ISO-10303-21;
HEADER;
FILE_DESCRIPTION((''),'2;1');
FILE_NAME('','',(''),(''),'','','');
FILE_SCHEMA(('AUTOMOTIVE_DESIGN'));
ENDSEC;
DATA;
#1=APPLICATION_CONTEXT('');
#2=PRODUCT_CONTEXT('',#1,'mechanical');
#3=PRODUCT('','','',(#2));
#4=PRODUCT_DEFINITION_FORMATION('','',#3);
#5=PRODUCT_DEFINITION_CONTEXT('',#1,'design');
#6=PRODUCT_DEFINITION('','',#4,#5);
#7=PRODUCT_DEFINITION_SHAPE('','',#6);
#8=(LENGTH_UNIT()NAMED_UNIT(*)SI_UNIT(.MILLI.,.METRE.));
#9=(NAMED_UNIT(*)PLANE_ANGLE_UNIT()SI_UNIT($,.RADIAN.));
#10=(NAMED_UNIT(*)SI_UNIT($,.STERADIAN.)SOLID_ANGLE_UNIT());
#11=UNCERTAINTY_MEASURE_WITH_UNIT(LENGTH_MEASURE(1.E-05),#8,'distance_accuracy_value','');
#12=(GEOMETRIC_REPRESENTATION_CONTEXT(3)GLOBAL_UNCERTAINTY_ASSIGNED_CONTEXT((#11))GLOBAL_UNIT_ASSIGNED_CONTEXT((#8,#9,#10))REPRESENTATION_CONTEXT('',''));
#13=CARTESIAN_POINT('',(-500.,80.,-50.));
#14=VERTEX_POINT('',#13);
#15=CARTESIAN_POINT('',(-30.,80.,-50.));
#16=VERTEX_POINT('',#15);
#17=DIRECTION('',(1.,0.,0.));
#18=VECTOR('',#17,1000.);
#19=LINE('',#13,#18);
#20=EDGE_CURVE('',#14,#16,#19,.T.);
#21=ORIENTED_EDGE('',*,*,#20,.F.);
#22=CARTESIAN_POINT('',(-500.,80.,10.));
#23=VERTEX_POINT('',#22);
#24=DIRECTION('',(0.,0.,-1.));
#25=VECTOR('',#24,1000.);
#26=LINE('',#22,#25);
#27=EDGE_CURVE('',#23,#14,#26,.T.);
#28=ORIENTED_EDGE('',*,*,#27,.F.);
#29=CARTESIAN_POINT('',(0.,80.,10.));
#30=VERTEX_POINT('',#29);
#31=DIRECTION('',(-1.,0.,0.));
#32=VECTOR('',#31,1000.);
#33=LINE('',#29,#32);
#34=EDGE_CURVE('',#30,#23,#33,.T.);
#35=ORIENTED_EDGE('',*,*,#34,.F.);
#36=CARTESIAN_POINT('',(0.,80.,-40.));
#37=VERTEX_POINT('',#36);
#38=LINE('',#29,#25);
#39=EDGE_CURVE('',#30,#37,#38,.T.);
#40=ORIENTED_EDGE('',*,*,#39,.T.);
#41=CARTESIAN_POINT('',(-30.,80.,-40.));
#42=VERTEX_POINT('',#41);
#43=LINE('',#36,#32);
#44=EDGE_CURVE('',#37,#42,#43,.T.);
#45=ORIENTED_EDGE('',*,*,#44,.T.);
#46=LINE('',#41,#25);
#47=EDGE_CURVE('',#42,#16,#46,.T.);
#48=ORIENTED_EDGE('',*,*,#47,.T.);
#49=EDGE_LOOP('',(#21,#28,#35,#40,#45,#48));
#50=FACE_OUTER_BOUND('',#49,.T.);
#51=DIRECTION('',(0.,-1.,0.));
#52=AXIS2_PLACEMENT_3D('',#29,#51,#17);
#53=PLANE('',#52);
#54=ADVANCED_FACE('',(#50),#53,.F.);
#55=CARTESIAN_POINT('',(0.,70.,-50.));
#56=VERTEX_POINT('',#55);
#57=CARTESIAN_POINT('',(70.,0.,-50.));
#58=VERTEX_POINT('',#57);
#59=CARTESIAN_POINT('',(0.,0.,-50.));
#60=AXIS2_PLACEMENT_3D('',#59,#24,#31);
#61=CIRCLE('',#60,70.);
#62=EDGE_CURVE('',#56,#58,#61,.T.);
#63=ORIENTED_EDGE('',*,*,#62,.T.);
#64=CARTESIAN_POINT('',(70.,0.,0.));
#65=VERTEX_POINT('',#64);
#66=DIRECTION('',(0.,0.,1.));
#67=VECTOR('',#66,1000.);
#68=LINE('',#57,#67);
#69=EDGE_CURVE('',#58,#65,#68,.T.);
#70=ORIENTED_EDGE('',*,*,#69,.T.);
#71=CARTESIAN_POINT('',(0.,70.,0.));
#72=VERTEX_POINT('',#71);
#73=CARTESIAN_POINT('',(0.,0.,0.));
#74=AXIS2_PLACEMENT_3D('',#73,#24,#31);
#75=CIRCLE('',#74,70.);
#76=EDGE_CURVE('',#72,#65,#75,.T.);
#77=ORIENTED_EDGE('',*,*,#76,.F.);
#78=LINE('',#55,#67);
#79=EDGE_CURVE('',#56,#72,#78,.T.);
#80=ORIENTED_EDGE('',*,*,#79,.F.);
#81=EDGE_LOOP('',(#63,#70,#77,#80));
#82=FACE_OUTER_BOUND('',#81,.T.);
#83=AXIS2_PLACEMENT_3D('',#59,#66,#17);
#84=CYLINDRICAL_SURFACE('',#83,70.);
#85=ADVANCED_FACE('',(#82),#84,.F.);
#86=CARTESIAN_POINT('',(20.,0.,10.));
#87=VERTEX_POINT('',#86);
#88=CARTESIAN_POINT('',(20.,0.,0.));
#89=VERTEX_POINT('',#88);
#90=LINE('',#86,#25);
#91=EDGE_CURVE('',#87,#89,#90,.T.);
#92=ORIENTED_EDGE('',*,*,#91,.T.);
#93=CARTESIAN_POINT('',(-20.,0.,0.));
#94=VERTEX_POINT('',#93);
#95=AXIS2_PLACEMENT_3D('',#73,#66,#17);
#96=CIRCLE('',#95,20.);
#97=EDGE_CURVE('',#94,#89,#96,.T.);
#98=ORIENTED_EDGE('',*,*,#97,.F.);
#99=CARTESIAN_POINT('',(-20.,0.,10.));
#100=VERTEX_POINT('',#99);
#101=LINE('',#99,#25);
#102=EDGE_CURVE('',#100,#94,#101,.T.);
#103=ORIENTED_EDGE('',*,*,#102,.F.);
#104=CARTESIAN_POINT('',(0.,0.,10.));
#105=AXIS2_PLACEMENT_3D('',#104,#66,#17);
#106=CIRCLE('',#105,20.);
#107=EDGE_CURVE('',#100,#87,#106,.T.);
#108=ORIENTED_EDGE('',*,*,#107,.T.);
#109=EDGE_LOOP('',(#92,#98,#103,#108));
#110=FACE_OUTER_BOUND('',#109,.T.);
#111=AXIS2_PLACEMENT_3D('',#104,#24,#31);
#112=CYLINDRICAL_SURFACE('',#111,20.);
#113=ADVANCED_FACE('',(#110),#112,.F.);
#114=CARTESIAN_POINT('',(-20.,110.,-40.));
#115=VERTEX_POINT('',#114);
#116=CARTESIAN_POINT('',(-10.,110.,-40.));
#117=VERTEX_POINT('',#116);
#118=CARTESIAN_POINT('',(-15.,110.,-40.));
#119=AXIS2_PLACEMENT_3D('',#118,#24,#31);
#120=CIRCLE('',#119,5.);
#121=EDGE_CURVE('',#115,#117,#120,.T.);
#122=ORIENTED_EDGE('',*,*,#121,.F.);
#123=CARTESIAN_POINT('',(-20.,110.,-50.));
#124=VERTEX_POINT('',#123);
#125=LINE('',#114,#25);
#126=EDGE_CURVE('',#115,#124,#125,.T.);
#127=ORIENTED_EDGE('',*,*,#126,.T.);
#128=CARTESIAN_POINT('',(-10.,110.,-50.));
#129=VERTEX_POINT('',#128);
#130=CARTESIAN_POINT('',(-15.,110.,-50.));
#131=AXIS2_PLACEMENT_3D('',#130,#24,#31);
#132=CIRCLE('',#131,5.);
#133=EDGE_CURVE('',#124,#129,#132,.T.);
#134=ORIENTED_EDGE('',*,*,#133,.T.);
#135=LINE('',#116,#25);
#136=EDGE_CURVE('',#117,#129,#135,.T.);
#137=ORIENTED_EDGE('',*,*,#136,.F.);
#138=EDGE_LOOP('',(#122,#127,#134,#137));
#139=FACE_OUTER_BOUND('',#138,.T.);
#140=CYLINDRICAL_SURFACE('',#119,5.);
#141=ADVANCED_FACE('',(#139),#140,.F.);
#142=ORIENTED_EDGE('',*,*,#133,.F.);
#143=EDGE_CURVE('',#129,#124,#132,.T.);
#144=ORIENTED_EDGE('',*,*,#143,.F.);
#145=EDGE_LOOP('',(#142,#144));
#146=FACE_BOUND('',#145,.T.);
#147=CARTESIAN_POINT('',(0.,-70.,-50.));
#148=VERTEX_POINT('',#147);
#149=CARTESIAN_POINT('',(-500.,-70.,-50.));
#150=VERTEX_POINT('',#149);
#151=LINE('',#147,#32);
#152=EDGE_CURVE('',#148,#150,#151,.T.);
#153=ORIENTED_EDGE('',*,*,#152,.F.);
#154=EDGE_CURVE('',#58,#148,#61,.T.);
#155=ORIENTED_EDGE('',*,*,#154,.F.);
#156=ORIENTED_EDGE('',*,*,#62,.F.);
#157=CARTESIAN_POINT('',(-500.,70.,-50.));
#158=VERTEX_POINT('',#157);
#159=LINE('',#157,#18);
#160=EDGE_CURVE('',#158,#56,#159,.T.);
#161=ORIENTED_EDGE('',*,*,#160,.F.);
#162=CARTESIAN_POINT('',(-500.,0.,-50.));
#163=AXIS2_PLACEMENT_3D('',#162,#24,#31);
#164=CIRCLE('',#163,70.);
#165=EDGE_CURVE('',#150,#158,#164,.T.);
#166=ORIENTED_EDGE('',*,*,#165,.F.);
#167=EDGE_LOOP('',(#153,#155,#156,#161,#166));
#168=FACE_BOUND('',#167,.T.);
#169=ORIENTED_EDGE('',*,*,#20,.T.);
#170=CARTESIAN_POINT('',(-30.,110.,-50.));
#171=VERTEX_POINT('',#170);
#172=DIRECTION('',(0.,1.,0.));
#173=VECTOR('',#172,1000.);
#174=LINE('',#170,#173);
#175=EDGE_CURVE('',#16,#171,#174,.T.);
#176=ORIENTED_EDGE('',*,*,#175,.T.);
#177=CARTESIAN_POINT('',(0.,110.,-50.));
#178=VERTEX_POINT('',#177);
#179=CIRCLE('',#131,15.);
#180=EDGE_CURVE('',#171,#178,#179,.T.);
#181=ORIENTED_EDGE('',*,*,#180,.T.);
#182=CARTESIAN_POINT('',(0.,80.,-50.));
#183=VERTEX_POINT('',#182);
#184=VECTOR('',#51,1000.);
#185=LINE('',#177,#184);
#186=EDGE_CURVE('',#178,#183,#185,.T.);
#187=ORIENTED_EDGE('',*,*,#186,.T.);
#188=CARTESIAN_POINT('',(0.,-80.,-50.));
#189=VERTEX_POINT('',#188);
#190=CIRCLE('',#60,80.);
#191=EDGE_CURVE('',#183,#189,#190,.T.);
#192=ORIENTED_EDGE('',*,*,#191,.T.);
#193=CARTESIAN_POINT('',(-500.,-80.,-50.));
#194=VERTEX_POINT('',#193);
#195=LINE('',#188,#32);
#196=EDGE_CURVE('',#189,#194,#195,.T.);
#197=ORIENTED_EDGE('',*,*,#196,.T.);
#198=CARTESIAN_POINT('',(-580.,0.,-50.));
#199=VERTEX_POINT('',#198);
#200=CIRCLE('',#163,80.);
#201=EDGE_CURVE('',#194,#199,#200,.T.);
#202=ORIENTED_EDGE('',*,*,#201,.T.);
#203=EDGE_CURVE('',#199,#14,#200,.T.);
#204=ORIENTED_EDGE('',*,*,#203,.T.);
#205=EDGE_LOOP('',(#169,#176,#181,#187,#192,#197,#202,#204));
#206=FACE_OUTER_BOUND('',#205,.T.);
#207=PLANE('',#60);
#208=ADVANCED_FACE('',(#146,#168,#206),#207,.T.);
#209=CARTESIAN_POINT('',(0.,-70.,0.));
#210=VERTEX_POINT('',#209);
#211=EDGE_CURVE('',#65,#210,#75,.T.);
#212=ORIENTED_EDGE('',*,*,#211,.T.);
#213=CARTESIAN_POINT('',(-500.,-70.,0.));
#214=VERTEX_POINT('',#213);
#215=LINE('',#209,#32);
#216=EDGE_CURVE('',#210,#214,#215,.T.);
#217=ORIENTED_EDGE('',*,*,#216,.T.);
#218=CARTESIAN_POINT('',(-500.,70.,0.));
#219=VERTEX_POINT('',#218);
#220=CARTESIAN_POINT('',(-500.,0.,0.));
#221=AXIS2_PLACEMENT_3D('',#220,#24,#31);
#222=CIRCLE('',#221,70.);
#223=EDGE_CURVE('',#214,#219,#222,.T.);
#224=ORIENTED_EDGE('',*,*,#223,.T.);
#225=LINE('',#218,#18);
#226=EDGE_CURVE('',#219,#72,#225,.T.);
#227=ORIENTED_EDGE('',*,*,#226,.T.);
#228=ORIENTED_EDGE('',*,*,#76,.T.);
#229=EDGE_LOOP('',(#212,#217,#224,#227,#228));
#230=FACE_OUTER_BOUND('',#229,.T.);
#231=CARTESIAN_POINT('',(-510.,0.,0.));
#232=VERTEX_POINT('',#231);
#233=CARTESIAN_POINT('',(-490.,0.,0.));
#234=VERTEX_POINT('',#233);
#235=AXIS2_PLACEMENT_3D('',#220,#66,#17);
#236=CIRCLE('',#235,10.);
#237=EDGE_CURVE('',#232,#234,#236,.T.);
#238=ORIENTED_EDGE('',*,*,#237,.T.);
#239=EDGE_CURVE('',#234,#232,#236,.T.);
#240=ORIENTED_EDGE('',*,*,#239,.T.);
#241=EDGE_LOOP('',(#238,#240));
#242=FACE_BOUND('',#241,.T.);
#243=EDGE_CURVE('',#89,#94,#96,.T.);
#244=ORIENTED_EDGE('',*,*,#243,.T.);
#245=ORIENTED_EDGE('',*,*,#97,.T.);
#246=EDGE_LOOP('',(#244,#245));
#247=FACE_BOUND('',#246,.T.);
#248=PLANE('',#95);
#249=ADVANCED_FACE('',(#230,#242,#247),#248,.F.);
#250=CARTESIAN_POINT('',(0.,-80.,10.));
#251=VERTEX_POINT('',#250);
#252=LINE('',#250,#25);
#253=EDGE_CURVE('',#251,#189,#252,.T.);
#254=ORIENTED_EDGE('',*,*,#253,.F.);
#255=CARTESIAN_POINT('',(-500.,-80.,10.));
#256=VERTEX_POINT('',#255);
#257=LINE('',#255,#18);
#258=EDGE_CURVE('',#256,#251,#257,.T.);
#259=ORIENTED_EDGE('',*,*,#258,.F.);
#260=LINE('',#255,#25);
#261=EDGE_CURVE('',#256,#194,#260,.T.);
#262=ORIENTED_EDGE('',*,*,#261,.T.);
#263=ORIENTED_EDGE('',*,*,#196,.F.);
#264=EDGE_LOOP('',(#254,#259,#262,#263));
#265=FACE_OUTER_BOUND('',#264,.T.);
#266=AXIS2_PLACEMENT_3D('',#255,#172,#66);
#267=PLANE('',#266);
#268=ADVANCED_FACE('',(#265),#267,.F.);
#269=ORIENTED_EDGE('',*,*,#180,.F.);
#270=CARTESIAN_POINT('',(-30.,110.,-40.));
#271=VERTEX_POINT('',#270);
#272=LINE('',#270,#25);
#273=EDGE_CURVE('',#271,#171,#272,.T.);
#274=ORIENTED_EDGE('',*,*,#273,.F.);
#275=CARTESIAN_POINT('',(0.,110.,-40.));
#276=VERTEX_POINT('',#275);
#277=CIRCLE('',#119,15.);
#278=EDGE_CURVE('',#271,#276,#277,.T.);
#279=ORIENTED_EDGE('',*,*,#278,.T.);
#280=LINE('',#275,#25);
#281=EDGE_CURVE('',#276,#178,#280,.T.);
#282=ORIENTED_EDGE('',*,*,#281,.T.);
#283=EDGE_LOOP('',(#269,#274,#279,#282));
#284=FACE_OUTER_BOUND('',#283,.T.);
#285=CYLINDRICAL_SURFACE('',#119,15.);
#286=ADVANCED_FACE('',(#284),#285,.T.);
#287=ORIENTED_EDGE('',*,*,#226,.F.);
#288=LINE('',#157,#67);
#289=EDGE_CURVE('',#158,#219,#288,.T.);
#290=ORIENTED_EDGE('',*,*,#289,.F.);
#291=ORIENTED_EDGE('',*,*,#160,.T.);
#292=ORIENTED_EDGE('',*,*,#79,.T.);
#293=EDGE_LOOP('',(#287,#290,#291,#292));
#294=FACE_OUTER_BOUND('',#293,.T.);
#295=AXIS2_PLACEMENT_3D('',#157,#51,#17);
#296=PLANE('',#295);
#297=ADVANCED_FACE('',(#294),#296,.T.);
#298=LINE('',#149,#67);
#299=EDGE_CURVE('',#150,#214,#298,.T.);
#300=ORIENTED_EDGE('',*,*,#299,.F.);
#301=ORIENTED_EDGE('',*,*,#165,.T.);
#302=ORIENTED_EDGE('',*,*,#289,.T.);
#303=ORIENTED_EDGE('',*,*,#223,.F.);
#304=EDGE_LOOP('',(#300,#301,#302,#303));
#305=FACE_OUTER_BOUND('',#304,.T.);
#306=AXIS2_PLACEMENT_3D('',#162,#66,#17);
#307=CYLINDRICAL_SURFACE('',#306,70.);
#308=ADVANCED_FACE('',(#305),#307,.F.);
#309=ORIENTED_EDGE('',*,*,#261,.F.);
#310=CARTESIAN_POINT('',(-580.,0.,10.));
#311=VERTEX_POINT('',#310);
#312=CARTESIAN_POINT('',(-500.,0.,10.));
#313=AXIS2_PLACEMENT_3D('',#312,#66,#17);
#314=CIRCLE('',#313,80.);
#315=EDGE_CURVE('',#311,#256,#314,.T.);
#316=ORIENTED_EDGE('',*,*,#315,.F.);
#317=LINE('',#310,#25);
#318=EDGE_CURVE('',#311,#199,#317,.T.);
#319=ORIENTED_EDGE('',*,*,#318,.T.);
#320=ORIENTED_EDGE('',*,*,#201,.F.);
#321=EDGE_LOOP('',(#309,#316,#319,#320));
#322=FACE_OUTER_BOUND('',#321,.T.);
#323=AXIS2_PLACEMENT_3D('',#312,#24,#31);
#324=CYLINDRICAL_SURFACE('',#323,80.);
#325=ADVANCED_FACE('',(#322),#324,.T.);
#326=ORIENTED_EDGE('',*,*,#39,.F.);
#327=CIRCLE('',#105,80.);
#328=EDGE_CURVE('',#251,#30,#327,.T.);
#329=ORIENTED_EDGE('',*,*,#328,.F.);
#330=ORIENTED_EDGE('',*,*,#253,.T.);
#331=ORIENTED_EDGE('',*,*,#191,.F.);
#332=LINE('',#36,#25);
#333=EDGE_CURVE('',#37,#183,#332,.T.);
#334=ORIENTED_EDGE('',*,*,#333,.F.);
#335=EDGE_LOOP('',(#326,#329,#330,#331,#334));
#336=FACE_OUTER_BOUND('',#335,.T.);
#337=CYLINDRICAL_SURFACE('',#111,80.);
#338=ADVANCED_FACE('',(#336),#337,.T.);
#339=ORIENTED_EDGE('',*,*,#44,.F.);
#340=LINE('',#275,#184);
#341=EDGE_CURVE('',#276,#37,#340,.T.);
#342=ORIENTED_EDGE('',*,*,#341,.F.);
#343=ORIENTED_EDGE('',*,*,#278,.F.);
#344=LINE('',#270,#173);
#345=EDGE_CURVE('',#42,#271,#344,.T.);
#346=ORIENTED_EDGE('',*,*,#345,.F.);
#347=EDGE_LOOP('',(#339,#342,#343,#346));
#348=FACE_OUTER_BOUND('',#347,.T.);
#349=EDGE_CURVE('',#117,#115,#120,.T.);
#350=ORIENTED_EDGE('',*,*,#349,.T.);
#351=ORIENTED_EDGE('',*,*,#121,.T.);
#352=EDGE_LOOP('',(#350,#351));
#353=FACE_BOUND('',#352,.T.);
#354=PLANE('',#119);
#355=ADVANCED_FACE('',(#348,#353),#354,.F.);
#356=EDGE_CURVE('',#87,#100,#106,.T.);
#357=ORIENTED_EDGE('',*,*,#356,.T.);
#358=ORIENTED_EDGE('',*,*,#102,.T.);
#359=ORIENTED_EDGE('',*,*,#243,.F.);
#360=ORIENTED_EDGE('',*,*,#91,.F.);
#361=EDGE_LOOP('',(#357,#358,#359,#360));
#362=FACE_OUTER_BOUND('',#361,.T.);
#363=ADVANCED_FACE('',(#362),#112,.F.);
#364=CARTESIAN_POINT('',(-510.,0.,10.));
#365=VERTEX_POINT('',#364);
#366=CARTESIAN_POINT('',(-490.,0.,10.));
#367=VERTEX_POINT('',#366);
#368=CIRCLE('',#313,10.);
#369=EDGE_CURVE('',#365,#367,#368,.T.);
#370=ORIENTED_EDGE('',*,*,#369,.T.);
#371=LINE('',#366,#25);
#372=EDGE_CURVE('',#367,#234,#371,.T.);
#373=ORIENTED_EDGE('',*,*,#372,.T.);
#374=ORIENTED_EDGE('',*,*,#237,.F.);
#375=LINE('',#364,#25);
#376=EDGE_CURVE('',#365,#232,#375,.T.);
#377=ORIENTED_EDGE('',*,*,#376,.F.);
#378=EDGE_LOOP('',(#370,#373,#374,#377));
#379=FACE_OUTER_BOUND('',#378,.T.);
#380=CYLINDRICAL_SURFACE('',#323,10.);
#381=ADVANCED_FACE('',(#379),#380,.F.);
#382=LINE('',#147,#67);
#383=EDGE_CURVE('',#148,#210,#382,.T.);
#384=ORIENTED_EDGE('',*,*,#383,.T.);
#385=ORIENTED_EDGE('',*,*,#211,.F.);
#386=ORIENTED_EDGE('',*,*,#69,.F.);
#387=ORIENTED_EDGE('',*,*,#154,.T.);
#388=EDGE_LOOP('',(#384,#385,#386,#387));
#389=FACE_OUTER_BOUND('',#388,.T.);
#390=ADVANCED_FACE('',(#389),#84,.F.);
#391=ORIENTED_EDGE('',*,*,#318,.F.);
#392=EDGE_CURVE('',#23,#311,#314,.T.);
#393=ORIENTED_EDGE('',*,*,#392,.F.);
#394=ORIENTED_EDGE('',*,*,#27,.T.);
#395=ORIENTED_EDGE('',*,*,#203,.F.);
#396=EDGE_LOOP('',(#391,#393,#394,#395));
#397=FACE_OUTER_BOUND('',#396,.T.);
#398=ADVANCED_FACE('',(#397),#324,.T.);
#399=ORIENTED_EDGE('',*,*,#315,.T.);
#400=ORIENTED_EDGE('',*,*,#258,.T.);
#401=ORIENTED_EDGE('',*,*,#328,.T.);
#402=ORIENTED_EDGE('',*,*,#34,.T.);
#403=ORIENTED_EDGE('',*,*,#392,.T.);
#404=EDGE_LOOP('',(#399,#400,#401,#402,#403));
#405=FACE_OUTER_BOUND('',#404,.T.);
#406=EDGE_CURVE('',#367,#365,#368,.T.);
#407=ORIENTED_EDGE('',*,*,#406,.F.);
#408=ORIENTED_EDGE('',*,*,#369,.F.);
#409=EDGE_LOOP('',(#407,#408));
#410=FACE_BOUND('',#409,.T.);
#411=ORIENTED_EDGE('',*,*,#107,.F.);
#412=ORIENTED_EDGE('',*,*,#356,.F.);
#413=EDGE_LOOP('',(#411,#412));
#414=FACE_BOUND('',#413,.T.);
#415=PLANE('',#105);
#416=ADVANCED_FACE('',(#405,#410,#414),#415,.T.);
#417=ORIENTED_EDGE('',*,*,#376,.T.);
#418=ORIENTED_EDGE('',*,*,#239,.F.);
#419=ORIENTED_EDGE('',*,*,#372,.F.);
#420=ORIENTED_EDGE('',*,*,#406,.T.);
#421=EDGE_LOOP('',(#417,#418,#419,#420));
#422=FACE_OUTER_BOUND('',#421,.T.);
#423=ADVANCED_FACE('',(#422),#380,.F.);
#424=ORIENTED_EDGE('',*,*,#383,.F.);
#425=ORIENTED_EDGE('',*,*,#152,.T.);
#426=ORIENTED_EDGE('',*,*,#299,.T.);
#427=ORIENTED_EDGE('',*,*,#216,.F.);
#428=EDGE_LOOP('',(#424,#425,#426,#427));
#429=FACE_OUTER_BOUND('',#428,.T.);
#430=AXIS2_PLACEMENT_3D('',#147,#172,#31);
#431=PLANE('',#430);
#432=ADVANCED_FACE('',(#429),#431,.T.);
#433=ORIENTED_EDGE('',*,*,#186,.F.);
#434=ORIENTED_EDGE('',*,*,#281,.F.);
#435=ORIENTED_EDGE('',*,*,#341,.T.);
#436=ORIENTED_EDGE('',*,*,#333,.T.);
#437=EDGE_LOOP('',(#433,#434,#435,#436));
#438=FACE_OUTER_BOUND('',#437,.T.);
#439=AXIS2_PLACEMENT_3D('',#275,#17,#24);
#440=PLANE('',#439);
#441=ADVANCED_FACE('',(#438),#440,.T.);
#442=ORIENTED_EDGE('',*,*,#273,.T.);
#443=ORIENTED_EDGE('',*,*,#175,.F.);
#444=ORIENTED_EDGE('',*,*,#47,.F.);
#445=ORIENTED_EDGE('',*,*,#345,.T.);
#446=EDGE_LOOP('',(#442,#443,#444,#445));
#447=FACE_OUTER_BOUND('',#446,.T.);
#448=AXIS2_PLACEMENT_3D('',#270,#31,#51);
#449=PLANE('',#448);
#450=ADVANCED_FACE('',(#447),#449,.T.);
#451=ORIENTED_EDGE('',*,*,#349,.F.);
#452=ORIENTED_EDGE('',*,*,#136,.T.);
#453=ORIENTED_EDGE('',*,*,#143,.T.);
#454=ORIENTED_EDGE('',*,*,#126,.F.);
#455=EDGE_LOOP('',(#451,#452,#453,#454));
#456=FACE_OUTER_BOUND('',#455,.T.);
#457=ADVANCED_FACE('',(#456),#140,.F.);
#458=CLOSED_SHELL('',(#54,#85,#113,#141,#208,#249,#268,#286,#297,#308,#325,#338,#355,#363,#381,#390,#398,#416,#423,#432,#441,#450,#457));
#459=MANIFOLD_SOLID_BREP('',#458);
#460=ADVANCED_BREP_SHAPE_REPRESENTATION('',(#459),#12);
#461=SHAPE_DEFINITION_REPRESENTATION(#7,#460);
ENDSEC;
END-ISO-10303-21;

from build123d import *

# Parameters (mm, degrees)
SKETCH_1_R      = 20
SKETCH_1_R_2    = 10
EXTRUDE_1_DEPTH = 10
EXTRUDE_START   = 50
EXTRUDE_2_DEPTH = 50
SKETCH_4_R      = 5
EXTRUDE_3_DEPTH = 10


with BuildPart() as part:
    # 草图1 → 凸台-拉伸1 (new body)
    with BuildSketch(Plane.XY):
        with BuildLine():
            Line((0, 80), (-500, 80))
            ThreePointArc((-500, 80), (-580, 0), (-500, -80))
            Line((-500, -80), (0, -80))
            ThreePointArc((0, -80), (80, 0), (0, 80))
        make_face()
        Circle(SKETCH_1_R, mode=Mode.SUBTRACT)
        with Locations((-500, 0)):
            Circle(SKETCH_1_R_2, mode=Mode.SUBTRACT)
    extrude(amount=EXTRUDE_1_DEPTH)

    # 草图2 → 凸台-拉伸2 (add)
    with BuildSketch(Plane(origin=(0, 0, 0), x_dir=(-1, 0, 0), z_dir=(0, 0, -1)).offset(EXTRUDE_START)):
        with BuildLine():
            Line((0, -80), (500, -80))
            ThreePointArc((500, -80), (580, 0), (500, 80))
            Line((500, 80), (0, 80))
            ThreePointArc((0, 80), (-80, 0), (0, -80))
        make_face()
        with BuildLine():
            Line((0, -70), (500, -70))
            ThreePointArc((500, -70), (570, 0), (500, 70))
            Line((500, 70), (0, 70))
            ThreePointArc((0, 70), (-70, 0), (0, -70))
        make_face(mode=Mode.SUBTRACT)
    extrude(amount=-EXTRUDE_2_DEPTH)

    # 草图4 → 凸台-拉伸3 (add)
    with BuildSketch(Plane(origin=(0, 0, -50), x_dir=(-1, 0, 0), z_dir=(0, 0, -1))):
        with BuildLine():
            Line((0, 110), (0, 80))
            Line((0, 80), (30, 80))
            Line((30, 80), (30, 110))
            ThreePointArc((30, 110), (15, 125), (0, 110))
        make_face()
        with Locations((15, 110)):
            Circle(SKETCH_4_R, mode=Mode.SUBTRACT)
    extrude(amount=-EXTRUDE_3_DEPTH)


solid = part.part
